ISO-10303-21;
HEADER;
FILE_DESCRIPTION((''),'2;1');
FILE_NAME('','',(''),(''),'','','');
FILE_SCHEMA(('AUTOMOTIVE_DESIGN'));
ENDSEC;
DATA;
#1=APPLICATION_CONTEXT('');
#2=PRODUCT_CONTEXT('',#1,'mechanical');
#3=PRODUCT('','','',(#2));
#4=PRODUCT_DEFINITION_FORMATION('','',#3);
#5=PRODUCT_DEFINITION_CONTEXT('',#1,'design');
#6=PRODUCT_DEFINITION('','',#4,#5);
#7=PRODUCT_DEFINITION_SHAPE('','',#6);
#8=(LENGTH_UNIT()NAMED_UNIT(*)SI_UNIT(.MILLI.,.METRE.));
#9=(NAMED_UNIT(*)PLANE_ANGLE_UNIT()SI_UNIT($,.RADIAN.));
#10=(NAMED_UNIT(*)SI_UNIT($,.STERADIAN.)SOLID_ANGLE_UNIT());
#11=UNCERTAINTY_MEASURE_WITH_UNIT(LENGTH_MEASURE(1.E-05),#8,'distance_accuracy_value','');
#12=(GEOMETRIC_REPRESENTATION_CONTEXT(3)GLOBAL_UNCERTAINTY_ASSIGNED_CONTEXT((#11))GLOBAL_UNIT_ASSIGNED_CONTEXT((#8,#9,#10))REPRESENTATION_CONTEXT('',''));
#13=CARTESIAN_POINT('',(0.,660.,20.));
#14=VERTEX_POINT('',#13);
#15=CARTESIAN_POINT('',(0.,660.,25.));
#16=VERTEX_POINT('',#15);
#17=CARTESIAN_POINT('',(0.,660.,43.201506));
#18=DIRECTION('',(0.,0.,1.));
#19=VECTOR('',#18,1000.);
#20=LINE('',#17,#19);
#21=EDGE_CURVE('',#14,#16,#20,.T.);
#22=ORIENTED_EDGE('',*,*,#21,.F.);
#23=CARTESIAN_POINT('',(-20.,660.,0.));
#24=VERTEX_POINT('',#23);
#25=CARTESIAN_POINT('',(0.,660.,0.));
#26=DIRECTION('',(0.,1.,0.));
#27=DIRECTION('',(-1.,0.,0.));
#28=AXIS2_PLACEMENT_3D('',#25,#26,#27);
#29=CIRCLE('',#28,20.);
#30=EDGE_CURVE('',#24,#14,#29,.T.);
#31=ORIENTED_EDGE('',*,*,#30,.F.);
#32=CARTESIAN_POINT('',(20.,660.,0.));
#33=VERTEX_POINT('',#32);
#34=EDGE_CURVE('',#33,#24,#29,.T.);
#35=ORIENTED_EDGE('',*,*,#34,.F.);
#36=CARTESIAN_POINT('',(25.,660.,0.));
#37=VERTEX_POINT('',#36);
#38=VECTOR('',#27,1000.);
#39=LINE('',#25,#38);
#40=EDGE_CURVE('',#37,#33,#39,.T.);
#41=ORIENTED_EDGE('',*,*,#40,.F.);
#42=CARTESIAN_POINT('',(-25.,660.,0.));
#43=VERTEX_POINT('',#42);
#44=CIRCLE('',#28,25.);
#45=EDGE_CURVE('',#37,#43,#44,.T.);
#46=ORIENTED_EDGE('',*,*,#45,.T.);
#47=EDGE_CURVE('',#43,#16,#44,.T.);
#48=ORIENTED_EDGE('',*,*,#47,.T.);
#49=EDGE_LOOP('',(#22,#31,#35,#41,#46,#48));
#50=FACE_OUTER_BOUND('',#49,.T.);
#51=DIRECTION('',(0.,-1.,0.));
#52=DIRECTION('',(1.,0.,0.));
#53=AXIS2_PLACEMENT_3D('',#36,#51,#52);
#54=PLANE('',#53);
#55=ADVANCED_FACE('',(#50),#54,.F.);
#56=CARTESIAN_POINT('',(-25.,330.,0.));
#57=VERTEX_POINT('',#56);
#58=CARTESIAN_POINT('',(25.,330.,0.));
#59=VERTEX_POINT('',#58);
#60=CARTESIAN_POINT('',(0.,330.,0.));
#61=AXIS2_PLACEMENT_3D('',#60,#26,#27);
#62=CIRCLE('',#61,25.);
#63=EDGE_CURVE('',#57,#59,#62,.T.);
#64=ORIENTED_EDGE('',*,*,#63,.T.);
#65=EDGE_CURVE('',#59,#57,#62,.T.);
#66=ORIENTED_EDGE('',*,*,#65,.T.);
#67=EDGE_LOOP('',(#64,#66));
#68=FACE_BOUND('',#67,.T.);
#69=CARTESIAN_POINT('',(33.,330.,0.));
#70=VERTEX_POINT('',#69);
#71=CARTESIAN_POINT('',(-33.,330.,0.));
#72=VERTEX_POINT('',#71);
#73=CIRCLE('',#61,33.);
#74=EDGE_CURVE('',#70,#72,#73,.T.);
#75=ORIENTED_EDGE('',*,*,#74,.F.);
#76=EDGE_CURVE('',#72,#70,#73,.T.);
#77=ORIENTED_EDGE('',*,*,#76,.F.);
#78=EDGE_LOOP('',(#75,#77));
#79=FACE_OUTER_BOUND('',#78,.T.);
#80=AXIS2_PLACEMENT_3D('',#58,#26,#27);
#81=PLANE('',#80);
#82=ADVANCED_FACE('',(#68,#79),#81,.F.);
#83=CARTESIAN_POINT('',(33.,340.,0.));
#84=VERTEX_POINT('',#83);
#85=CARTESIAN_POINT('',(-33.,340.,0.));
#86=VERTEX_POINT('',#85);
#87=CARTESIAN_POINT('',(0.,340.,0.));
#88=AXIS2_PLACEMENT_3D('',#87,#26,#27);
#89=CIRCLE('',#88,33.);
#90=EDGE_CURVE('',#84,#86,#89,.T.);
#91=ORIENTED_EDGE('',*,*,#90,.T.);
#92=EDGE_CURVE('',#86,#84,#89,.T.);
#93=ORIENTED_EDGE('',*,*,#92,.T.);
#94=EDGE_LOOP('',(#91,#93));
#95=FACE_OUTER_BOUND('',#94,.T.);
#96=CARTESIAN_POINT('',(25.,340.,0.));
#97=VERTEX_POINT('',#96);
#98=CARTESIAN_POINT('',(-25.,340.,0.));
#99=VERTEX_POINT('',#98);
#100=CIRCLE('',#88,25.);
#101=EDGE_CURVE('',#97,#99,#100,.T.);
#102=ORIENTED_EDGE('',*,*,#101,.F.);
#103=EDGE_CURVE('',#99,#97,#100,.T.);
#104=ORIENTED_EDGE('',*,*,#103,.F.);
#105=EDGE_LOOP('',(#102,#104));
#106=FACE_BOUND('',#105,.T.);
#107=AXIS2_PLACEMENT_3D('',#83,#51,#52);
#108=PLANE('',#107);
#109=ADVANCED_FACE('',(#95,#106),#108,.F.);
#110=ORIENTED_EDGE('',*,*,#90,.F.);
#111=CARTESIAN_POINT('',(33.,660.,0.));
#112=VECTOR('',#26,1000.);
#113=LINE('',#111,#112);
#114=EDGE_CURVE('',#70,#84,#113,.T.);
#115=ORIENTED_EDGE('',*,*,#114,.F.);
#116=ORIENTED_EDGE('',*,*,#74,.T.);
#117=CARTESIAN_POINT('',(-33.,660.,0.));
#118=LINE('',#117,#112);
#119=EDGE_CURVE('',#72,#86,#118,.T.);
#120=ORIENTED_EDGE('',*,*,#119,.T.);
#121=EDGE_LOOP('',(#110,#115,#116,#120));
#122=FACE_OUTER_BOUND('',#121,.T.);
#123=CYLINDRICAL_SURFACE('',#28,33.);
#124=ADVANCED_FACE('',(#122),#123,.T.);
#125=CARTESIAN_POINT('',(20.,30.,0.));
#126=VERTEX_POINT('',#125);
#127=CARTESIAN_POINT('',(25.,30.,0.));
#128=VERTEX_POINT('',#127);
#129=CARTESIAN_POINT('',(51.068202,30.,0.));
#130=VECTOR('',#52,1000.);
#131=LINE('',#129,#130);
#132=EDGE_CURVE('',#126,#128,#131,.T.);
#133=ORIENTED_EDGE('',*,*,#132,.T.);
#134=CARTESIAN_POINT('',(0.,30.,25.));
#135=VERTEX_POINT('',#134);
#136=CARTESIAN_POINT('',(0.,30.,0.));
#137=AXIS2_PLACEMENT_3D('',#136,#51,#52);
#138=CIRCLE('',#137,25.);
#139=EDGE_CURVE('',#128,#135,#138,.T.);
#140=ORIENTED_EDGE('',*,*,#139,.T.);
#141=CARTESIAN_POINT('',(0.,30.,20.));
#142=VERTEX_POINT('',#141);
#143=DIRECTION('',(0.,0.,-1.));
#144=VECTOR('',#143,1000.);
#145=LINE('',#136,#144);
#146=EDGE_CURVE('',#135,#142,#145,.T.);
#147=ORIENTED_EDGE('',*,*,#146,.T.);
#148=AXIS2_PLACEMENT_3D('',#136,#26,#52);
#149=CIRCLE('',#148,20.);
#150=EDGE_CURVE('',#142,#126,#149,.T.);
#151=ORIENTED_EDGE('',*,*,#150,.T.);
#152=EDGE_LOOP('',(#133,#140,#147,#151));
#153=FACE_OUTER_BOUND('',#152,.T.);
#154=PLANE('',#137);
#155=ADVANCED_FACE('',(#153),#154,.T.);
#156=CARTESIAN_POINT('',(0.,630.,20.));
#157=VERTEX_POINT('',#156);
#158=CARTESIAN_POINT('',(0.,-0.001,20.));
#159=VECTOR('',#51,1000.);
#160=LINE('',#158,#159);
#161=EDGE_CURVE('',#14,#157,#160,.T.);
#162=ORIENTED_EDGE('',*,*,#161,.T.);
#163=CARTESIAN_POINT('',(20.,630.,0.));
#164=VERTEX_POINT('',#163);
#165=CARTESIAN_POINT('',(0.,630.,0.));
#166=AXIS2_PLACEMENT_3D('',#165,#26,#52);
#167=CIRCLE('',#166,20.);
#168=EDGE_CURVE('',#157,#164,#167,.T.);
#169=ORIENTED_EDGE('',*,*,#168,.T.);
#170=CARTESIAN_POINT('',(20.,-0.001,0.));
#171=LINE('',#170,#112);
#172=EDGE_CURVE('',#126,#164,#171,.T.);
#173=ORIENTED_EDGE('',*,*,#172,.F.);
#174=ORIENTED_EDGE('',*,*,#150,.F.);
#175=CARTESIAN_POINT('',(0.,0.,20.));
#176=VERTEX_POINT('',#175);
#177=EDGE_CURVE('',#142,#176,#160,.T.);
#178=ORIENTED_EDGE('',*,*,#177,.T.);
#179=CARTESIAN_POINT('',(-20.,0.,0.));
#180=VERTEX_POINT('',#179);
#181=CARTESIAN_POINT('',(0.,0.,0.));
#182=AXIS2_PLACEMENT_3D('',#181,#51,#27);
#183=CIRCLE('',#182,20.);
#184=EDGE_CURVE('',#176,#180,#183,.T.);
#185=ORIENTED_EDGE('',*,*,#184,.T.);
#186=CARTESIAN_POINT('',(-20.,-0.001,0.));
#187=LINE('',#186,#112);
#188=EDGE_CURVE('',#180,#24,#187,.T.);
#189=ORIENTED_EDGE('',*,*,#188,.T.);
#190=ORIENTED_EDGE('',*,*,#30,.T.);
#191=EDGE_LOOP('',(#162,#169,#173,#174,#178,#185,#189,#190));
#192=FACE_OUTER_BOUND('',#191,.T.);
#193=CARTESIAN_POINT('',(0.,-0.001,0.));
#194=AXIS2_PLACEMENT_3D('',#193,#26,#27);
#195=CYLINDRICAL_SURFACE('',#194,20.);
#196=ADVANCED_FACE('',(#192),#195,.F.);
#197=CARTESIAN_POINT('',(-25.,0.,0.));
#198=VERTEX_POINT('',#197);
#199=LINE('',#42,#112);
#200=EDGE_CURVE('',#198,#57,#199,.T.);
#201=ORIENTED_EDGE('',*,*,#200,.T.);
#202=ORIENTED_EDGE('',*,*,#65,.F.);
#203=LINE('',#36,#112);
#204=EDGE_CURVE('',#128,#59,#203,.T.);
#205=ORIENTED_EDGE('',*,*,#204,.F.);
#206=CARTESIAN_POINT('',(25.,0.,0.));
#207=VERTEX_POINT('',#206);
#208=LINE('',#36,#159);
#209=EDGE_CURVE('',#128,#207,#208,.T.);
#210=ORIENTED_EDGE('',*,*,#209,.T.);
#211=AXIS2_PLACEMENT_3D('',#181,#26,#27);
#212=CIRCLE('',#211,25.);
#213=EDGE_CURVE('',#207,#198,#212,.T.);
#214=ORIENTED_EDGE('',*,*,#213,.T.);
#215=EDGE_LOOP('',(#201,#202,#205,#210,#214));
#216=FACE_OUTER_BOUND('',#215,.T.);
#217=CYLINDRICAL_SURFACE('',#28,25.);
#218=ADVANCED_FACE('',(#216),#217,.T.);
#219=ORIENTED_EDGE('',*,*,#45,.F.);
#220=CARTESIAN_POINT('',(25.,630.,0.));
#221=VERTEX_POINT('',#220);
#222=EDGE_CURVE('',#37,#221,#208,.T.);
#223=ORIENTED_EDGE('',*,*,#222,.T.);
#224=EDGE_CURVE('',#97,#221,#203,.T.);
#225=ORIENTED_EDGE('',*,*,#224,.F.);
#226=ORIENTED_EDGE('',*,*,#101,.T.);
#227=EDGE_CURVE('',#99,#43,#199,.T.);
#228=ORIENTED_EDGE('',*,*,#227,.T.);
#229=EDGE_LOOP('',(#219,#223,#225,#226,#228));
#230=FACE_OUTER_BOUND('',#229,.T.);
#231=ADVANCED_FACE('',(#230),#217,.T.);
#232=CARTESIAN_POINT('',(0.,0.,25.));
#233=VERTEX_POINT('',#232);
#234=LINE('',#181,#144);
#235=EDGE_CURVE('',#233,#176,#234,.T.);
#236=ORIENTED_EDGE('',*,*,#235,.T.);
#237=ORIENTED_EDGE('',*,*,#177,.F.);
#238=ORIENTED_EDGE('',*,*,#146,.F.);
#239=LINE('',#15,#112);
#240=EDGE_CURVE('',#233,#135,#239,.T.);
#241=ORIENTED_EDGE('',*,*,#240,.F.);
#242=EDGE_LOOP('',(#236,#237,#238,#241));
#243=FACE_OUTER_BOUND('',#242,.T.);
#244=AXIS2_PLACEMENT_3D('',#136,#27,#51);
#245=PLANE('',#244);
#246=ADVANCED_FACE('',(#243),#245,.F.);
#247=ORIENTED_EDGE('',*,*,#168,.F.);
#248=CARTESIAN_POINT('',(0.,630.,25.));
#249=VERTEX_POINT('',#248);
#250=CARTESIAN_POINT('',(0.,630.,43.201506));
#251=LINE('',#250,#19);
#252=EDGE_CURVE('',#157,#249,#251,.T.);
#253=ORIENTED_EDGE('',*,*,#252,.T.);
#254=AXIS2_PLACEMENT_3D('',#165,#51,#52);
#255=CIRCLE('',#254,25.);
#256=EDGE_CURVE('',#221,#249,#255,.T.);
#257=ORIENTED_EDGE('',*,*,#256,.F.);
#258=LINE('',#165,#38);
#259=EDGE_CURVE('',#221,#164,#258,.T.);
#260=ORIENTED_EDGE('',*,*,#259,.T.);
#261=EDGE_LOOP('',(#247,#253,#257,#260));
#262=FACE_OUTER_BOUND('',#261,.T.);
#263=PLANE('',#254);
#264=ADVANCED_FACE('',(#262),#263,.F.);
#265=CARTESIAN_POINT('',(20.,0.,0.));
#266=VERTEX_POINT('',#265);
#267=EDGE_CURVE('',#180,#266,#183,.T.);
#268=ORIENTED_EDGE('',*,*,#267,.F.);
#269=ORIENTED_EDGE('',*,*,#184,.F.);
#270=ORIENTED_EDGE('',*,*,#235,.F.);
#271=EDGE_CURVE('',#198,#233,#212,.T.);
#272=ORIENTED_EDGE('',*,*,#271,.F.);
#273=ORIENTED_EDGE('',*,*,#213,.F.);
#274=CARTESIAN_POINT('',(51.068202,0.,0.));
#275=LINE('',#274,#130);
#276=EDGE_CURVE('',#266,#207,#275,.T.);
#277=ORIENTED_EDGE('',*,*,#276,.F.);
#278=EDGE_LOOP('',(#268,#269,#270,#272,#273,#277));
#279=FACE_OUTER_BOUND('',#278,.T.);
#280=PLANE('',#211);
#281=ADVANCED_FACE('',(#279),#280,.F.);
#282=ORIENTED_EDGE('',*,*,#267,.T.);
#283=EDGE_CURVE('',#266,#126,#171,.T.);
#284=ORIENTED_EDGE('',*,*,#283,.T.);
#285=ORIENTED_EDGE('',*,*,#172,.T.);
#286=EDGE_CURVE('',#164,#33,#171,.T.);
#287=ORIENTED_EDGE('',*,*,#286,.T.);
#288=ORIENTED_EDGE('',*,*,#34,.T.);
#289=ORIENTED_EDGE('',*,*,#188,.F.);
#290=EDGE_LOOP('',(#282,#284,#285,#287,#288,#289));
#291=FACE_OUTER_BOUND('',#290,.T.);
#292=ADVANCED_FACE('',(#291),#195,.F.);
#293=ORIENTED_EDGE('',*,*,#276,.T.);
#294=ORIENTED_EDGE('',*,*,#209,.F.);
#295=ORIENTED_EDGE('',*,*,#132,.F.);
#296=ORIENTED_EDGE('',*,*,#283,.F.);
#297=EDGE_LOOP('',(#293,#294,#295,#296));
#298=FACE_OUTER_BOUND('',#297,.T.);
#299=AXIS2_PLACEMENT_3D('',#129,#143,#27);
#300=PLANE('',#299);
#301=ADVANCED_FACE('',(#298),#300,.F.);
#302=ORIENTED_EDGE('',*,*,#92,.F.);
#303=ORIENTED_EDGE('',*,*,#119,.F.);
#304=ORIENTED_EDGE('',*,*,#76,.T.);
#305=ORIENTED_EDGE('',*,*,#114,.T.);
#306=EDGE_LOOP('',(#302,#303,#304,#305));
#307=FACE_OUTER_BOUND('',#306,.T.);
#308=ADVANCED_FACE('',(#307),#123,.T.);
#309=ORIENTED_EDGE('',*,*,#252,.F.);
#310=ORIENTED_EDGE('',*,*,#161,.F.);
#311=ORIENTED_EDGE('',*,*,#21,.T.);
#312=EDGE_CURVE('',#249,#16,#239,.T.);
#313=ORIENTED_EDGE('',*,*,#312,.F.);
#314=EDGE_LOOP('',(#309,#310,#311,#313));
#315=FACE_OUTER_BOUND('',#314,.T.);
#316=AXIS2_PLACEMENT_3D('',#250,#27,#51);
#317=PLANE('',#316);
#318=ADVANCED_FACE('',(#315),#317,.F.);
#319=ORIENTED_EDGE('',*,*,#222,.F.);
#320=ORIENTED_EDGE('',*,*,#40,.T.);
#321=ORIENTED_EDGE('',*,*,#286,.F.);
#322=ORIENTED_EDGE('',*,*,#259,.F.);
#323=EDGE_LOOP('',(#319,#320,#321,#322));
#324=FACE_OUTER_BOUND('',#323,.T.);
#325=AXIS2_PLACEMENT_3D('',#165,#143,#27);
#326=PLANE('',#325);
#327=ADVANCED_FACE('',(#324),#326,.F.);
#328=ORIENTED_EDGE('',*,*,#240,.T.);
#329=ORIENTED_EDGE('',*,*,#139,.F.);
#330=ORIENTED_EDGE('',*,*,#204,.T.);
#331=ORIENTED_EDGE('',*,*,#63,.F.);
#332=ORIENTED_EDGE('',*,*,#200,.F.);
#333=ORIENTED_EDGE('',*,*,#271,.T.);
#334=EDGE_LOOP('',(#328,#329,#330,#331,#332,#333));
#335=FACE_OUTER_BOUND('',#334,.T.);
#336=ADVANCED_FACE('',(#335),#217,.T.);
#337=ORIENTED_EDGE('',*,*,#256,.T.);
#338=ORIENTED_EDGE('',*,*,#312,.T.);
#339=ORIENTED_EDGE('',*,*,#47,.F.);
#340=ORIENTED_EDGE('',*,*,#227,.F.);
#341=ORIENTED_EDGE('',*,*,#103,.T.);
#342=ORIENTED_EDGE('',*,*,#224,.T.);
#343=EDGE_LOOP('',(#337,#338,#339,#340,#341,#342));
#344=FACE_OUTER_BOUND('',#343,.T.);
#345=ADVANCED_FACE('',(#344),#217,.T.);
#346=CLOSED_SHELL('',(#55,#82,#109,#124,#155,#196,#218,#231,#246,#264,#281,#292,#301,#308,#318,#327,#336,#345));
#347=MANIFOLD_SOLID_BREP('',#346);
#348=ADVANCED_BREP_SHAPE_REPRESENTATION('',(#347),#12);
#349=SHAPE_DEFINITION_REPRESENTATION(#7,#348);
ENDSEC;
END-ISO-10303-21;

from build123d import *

# Parameters (mm, degrees)
CUT_EXTRUDE1_REACH = 663.648
SKETCH2_R          = 20
CUT_EXTRUDE2_DEPTH = 30
CUT_EXTRUDE3_DEPTH = 30


with BuildPart() as part:
    # Sketch1 → Revolve1 (revolve)
    with BuildSketch(Plane.XY, mode=Mode.PRIVATE) as revolve1_sk:
        Polygon((0, 0), (25, 0), (25, 330), (33, 330), (33, 340), (25, 340), (25, 585.119663834), (25, 619.032357738), (25, 660), (0, 660), align=None)
    revolve(revolve1_sk.sketch.rotate(Axis((0, 660, 0), (0, -1, 0)), 180), axis=Axis((0, 660, 0), (0, -1, 0)))

    # Sketch2 → Cut-Extrude1 (cut, up to next)
    with BuildSketch(Plane(origin=(0, 660, 0), x_dir=(1, 0, 0), z_dir=(0, 1, 0)), mode=Mode.PRIVATE) as cut_extrude1_sk1:
        with Locations(Location((0, 0, 0), (0, 0, 180))):
            Circle(SKETCH2_R)
    cut_extrude1_tool1 = extrude(cut_extrude1_sk1.sketch, amount=-CUT_EXTRUDE1_REACH, mode=Mode.PRIVATE) & part.part
    add(cut_extrude1_tool1.solids().sort_by_distance((0, 660, 0))[0], mode=Mode.SUBTRACT)

    # Sketch3 → Cut-Extrude2 (cut)
    with BuildSketch(Plane(origin=(0, 660, 0), x_dir=(1, 0, 0), z_dir=(0, 1, 0))):
        with BuildLine():
            Line((0, -43.201505936), (0, 0))
            Line((0, 0), (43.201505936, 0))
            ThreePointArc((43.201505936, 0), (30.548077804, -30.548077804), (0, -43.201505936))
        make_face()
    extrude(amount=-CUT_EXTRUDE2_DEPTH, mode=Mode.SUBTRACT)

    # Sketch4 → Cut-Extrude3 (cut)
    with BuildSketch(Plane.XZ):
        with BuildLine():
            Line((51.068202024, 0), (0, 0))
            Line((0, 0), (0, 51.068202024))
            ThreePointArc((0, 51.068202024), (36.110671954, 36.110671954), (51.068202024, 0))
        make_face()
    extrude(amount=-CUT_EXTRUDE3_DEPTH, mode=Mode.SUBTRACT)


solid = part.part
